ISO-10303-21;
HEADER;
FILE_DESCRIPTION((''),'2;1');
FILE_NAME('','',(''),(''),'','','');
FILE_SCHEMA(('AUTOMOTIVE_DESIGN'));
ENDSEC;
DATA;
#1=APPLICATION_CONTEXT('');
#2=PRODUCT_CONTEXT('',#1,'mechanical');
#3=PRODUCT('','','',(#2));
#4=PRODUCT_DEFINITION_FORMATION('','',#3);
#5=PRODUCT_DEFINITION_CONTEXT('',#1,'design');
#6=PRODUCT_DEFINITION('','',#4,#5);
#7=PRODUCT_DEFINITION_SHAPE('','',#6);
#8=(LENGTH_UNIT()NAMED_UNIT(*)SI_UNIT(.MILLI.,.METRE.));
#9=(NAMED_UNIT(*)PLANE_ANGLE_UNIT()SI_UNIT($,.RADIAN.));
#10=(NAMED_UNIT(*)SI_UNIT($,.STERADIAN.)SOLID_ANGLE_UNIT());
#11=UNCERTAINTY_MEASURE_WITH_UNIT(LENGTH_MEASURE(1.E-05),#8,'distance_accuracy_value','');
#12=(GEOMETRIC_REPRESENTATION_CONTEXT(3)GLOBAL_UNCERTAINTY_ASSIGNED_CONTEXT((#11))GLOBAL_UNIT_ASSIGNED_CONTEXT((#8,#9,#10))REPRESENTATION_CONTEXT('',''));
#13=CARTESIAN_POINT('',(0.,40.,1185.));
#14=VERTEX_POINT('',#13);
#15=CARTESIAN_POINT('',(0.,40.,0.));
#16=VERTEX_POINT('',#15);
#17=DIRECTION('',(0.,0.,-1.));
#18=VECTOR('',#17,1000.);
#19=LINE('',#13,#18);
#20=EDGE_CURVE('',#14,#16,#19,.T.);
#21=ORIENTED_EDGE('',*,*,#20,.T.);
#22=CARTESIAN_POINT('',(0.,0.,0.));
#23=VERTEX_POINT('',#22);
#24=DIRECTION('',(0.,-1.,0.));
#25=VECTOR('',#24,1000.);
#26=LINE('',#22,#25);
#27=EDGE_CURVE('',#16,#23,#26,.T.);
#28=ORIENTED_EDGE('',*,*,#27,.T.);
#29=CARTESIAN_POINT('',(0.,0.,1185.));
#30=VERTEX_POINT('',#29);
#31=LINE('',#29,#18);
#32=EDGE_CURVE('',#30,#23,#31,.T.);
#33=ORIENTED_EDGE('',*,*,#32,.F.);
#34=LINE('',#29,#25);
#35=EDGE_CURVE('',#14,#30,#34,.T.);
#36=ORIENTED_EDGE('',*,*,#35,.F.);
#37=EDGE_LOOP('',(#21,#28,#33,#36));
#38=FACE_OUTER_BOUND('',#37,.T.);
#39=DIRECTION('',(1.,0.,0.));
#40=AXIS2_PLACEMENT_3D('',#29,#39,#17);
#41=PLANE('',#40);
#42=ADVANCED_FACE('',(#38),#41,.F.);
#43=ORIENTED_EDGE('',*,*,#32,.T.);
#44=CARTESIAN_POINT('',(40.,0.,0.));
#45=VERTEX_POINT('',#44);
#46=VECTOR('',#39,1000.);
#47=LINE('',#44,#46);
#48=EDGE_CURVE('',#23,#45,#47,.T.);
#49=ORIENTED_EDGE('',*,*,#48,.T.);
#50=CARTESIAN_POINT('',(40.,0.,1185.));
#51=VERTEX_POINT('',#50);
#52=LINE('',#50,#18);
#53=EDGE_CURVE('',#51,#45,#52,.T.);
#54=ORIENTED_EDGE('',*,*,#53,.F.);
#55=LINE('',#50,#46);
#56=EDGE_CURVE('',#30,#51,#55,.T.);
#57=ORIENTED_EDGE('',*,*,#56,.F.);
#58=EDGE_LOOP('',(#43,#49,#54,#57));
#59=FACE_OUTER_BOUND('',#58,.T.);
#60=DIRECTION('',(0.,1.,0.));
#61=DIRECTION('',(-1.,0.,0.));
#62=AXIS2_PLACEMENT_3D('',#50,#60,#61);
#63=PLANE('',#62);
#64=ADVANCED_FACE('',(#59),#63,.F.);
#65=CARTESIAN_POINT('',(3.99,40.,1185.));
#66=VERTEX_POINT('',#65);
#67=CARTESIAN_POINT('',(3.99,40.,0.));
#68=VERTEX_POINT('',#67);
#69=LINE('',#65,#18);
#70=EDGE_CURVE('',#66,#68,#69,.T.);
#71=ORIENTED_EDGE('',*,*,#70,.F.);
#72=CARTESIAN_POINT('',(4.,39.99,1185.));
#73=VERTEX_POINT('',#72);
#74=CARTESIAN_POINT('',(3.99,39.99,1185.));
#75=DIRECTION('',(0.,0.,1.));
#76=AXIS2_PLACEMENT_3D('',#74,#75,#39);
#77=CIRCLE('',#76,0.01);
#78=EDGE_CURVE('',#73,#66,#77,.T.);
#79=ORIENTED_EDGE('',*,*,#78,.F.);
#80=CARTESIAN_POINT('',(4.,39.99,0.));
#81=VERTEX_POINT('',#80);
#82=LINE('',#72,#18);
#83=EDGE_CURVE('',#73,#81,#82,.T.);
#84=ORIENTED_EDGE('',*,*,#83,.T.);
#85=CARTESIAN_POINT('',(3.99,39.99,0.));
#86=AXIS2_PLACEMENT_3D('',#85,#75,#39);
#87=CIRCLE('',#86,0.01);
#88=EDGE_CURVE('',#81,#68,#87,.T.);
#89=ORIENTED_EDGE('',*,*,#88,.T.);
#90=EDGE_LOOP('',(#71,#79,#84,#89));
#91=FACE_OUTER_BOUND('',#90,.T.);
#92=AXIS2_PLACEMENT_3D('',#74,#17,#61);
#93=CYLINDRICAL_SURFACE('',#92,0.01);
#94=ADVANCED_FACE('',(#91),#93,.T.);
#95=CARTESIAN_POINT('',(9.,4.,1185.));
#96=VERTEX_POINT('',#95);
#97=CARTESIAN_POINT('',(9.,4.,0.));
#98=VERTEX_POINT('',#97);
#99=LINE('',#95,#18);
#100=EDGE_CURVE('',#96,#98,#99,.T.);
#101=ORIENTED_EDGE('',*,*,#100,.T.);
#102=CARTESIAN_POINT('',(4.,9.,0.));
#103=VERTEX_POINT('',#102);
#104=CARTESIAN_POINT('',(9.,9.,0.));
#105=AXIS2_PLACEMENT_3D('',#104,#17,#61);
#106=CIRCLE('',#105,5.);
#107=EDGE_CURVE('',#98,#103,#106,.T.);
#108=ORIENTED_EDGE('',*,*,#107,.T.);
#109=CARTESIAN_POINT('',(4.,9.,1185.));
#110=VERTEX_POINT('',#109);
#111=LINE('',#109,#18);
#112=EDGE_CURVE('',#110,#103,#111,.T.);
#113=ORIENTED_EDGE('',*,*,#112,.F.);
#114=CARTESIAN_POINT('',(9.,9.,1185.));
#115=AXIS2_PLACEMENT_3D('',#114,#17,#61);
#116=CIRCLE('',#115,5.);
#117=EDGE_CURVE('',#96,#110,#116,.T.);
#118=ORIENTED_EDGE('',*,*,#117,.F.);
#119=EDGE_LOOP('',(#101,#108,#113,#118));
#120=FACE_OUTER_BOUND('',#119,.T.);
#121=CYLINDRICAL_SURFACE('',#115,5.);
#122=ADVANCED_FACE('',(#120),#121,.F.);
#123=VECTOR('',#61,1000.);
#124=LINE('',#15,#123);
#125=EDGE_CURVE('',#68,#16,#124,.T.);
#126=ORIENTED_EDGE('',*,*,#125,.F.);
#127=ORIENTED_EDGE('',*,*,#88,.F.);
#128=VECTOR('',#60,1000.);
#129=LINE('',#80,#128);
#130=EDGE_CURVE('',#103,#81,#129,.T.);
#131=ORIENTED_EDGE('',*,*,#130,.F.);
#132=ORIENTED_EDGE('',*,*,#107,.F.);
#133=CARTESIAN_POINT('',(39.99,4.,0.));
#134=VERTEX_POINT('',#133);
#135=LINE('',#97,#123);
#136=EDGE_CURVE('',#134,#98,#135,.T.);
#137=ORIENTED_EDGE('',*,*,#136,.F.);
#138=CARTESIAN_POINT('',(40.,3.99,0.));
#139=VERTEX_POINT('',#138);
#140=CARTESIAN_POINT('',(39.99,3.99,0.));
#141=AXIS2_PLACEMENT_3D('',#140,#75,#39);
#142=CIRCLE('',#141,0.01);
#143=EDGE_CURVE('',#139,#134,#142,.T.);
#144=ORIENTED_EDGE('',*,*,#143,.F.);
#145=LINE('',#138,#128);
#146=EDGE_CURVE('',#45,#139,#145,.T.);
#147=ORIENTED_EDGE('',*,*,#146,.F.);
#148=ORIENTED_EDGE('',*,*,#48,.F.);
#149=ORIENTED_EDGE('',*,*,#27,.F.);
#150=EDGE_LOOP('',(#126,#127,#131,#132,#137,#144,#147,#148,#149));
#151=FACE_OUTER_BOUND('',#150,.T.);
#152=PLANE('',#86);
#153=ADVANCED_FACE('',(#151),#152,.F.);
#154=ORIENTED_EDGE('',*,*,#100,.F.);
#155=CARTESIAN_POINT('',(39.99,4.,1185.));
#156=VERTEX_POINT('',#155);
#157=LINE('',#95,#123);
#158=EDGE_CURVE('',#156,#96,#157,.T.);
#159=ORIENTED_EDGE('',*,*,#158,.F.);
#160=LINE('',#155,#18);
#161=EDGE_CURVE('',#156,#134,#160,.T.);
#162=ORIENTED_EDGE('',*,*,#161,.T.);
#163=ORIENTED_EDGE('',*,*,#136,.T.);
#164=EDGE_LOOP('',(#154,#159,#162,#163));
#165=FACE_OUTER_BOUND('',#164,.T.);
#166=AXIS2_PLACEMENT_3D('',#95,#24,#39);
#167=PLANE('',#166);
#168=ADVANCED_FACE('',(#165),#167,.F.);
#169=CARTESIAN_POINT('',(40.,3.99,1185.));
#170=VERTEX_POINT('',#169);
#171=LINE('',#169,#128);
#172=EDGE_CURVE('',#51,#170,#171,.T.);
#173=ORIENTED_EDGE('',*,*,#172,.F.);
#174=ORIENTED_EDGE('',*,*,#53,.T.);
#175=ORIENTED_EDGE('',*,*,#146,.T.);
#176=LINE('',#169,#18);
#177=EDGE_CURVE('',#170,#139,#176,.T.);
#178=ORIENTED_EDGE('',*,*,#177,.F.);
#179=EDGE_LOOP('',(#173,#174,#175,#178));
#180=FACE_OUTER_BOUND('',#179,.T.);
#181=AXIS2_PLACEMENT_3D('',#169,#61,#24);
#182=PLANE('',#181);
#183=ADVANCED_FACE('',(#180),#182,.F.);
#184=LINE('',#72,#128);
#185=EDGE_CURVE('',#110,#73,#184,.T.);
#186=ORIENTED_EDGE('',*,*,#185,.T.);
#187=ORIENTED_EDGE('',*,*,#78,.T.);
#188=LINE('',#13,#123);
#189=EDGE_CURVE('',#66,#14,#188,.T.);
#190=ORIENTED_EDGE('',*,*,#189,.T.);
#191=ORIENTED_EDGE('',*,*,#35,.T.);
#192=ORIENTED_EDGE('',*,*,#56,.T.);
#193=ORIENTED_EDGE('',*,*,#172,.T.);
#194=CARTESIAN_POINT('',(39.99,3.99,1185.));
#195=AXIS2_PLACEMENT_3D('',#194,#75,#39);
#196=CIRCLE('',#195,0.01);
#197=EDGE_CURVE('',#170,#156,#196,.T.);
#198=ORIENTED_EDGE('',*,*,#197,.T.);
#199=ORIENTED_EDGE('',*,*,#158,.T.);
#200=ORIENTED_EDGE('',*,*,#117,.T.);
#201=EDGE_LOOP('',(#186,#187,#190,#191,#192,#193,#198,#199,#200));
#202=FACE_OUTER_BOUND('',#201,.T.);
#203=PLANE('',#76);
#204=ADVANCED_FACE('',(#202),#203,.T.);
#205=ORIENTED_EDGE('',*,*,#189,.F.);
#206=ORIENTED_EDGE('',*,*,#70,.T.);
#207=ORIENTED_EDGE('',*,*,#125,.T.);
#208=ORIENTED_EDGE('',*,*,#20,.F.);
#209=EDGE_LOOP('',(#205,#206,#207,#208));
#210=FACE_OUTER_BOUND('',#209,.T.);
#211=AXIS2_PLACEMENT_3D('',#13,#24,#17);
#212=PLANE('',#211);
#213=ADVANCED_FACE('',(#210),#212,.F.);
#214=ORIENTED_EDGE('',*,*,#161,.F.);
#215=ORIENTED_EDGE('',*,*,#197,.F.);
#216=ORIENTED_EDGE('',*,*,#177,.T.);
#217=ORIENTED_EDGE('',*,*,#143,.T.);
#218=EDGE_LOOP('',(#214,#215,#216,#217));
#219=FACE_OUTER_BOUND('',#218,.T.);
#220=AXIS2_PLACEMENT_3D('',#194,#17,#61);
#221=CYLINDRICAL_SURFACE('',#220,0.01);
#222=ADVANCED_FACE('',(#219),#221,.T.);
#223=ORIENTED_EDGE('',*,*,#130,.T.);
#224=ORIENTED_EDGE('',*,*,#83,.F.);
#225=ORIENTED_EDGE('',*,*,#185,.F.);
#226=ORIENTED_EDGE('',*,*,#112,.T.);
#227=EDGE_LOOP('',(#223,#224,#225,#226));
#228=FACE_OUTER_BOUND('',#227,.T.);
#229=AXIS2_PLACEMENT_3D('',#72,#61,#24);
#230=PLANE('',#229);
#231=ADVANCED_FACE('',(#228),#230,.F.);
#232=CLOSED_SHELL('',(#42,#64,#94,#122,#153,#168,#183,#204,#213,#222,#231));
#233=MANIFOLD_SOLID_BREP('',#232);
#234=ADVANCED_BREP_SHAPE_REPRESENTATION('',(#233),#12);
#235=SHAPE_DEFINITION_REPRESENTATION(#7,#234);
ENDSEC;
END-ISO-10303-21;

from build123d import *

# Parameters (mm, degrees)
EXTRUDE_1_DEPTH = 1185


with BuildPart() as part:
    # 草图1 → 拉伸1 (new body)
    with BuildSketch(Plane.XY):
        with BuildLine():
            Line((0, 0), (0, 40))
            Line((0, 40), (3.99, 40))
            ThreePointArc((3.99, 40), (3.997071068, 39.997071068), (4, 39.99))
            Line((4, 39.99), (4, 9))
            ThreePointArc((4, 9), (5.464466094, 5.464466094), (9, 4))
            Line((9, 4), (39.99, 4))
            ThreePointArc((39.99, 4), (39.997071068, 3.997071068), (40, 3.99))
            Line((40, 3.99), (40, 0))
            Line((40, 0), (0, 0))
        make_face()
    extrude(amount=EXTRUDE_1_DEPTH)


solid = part.part
